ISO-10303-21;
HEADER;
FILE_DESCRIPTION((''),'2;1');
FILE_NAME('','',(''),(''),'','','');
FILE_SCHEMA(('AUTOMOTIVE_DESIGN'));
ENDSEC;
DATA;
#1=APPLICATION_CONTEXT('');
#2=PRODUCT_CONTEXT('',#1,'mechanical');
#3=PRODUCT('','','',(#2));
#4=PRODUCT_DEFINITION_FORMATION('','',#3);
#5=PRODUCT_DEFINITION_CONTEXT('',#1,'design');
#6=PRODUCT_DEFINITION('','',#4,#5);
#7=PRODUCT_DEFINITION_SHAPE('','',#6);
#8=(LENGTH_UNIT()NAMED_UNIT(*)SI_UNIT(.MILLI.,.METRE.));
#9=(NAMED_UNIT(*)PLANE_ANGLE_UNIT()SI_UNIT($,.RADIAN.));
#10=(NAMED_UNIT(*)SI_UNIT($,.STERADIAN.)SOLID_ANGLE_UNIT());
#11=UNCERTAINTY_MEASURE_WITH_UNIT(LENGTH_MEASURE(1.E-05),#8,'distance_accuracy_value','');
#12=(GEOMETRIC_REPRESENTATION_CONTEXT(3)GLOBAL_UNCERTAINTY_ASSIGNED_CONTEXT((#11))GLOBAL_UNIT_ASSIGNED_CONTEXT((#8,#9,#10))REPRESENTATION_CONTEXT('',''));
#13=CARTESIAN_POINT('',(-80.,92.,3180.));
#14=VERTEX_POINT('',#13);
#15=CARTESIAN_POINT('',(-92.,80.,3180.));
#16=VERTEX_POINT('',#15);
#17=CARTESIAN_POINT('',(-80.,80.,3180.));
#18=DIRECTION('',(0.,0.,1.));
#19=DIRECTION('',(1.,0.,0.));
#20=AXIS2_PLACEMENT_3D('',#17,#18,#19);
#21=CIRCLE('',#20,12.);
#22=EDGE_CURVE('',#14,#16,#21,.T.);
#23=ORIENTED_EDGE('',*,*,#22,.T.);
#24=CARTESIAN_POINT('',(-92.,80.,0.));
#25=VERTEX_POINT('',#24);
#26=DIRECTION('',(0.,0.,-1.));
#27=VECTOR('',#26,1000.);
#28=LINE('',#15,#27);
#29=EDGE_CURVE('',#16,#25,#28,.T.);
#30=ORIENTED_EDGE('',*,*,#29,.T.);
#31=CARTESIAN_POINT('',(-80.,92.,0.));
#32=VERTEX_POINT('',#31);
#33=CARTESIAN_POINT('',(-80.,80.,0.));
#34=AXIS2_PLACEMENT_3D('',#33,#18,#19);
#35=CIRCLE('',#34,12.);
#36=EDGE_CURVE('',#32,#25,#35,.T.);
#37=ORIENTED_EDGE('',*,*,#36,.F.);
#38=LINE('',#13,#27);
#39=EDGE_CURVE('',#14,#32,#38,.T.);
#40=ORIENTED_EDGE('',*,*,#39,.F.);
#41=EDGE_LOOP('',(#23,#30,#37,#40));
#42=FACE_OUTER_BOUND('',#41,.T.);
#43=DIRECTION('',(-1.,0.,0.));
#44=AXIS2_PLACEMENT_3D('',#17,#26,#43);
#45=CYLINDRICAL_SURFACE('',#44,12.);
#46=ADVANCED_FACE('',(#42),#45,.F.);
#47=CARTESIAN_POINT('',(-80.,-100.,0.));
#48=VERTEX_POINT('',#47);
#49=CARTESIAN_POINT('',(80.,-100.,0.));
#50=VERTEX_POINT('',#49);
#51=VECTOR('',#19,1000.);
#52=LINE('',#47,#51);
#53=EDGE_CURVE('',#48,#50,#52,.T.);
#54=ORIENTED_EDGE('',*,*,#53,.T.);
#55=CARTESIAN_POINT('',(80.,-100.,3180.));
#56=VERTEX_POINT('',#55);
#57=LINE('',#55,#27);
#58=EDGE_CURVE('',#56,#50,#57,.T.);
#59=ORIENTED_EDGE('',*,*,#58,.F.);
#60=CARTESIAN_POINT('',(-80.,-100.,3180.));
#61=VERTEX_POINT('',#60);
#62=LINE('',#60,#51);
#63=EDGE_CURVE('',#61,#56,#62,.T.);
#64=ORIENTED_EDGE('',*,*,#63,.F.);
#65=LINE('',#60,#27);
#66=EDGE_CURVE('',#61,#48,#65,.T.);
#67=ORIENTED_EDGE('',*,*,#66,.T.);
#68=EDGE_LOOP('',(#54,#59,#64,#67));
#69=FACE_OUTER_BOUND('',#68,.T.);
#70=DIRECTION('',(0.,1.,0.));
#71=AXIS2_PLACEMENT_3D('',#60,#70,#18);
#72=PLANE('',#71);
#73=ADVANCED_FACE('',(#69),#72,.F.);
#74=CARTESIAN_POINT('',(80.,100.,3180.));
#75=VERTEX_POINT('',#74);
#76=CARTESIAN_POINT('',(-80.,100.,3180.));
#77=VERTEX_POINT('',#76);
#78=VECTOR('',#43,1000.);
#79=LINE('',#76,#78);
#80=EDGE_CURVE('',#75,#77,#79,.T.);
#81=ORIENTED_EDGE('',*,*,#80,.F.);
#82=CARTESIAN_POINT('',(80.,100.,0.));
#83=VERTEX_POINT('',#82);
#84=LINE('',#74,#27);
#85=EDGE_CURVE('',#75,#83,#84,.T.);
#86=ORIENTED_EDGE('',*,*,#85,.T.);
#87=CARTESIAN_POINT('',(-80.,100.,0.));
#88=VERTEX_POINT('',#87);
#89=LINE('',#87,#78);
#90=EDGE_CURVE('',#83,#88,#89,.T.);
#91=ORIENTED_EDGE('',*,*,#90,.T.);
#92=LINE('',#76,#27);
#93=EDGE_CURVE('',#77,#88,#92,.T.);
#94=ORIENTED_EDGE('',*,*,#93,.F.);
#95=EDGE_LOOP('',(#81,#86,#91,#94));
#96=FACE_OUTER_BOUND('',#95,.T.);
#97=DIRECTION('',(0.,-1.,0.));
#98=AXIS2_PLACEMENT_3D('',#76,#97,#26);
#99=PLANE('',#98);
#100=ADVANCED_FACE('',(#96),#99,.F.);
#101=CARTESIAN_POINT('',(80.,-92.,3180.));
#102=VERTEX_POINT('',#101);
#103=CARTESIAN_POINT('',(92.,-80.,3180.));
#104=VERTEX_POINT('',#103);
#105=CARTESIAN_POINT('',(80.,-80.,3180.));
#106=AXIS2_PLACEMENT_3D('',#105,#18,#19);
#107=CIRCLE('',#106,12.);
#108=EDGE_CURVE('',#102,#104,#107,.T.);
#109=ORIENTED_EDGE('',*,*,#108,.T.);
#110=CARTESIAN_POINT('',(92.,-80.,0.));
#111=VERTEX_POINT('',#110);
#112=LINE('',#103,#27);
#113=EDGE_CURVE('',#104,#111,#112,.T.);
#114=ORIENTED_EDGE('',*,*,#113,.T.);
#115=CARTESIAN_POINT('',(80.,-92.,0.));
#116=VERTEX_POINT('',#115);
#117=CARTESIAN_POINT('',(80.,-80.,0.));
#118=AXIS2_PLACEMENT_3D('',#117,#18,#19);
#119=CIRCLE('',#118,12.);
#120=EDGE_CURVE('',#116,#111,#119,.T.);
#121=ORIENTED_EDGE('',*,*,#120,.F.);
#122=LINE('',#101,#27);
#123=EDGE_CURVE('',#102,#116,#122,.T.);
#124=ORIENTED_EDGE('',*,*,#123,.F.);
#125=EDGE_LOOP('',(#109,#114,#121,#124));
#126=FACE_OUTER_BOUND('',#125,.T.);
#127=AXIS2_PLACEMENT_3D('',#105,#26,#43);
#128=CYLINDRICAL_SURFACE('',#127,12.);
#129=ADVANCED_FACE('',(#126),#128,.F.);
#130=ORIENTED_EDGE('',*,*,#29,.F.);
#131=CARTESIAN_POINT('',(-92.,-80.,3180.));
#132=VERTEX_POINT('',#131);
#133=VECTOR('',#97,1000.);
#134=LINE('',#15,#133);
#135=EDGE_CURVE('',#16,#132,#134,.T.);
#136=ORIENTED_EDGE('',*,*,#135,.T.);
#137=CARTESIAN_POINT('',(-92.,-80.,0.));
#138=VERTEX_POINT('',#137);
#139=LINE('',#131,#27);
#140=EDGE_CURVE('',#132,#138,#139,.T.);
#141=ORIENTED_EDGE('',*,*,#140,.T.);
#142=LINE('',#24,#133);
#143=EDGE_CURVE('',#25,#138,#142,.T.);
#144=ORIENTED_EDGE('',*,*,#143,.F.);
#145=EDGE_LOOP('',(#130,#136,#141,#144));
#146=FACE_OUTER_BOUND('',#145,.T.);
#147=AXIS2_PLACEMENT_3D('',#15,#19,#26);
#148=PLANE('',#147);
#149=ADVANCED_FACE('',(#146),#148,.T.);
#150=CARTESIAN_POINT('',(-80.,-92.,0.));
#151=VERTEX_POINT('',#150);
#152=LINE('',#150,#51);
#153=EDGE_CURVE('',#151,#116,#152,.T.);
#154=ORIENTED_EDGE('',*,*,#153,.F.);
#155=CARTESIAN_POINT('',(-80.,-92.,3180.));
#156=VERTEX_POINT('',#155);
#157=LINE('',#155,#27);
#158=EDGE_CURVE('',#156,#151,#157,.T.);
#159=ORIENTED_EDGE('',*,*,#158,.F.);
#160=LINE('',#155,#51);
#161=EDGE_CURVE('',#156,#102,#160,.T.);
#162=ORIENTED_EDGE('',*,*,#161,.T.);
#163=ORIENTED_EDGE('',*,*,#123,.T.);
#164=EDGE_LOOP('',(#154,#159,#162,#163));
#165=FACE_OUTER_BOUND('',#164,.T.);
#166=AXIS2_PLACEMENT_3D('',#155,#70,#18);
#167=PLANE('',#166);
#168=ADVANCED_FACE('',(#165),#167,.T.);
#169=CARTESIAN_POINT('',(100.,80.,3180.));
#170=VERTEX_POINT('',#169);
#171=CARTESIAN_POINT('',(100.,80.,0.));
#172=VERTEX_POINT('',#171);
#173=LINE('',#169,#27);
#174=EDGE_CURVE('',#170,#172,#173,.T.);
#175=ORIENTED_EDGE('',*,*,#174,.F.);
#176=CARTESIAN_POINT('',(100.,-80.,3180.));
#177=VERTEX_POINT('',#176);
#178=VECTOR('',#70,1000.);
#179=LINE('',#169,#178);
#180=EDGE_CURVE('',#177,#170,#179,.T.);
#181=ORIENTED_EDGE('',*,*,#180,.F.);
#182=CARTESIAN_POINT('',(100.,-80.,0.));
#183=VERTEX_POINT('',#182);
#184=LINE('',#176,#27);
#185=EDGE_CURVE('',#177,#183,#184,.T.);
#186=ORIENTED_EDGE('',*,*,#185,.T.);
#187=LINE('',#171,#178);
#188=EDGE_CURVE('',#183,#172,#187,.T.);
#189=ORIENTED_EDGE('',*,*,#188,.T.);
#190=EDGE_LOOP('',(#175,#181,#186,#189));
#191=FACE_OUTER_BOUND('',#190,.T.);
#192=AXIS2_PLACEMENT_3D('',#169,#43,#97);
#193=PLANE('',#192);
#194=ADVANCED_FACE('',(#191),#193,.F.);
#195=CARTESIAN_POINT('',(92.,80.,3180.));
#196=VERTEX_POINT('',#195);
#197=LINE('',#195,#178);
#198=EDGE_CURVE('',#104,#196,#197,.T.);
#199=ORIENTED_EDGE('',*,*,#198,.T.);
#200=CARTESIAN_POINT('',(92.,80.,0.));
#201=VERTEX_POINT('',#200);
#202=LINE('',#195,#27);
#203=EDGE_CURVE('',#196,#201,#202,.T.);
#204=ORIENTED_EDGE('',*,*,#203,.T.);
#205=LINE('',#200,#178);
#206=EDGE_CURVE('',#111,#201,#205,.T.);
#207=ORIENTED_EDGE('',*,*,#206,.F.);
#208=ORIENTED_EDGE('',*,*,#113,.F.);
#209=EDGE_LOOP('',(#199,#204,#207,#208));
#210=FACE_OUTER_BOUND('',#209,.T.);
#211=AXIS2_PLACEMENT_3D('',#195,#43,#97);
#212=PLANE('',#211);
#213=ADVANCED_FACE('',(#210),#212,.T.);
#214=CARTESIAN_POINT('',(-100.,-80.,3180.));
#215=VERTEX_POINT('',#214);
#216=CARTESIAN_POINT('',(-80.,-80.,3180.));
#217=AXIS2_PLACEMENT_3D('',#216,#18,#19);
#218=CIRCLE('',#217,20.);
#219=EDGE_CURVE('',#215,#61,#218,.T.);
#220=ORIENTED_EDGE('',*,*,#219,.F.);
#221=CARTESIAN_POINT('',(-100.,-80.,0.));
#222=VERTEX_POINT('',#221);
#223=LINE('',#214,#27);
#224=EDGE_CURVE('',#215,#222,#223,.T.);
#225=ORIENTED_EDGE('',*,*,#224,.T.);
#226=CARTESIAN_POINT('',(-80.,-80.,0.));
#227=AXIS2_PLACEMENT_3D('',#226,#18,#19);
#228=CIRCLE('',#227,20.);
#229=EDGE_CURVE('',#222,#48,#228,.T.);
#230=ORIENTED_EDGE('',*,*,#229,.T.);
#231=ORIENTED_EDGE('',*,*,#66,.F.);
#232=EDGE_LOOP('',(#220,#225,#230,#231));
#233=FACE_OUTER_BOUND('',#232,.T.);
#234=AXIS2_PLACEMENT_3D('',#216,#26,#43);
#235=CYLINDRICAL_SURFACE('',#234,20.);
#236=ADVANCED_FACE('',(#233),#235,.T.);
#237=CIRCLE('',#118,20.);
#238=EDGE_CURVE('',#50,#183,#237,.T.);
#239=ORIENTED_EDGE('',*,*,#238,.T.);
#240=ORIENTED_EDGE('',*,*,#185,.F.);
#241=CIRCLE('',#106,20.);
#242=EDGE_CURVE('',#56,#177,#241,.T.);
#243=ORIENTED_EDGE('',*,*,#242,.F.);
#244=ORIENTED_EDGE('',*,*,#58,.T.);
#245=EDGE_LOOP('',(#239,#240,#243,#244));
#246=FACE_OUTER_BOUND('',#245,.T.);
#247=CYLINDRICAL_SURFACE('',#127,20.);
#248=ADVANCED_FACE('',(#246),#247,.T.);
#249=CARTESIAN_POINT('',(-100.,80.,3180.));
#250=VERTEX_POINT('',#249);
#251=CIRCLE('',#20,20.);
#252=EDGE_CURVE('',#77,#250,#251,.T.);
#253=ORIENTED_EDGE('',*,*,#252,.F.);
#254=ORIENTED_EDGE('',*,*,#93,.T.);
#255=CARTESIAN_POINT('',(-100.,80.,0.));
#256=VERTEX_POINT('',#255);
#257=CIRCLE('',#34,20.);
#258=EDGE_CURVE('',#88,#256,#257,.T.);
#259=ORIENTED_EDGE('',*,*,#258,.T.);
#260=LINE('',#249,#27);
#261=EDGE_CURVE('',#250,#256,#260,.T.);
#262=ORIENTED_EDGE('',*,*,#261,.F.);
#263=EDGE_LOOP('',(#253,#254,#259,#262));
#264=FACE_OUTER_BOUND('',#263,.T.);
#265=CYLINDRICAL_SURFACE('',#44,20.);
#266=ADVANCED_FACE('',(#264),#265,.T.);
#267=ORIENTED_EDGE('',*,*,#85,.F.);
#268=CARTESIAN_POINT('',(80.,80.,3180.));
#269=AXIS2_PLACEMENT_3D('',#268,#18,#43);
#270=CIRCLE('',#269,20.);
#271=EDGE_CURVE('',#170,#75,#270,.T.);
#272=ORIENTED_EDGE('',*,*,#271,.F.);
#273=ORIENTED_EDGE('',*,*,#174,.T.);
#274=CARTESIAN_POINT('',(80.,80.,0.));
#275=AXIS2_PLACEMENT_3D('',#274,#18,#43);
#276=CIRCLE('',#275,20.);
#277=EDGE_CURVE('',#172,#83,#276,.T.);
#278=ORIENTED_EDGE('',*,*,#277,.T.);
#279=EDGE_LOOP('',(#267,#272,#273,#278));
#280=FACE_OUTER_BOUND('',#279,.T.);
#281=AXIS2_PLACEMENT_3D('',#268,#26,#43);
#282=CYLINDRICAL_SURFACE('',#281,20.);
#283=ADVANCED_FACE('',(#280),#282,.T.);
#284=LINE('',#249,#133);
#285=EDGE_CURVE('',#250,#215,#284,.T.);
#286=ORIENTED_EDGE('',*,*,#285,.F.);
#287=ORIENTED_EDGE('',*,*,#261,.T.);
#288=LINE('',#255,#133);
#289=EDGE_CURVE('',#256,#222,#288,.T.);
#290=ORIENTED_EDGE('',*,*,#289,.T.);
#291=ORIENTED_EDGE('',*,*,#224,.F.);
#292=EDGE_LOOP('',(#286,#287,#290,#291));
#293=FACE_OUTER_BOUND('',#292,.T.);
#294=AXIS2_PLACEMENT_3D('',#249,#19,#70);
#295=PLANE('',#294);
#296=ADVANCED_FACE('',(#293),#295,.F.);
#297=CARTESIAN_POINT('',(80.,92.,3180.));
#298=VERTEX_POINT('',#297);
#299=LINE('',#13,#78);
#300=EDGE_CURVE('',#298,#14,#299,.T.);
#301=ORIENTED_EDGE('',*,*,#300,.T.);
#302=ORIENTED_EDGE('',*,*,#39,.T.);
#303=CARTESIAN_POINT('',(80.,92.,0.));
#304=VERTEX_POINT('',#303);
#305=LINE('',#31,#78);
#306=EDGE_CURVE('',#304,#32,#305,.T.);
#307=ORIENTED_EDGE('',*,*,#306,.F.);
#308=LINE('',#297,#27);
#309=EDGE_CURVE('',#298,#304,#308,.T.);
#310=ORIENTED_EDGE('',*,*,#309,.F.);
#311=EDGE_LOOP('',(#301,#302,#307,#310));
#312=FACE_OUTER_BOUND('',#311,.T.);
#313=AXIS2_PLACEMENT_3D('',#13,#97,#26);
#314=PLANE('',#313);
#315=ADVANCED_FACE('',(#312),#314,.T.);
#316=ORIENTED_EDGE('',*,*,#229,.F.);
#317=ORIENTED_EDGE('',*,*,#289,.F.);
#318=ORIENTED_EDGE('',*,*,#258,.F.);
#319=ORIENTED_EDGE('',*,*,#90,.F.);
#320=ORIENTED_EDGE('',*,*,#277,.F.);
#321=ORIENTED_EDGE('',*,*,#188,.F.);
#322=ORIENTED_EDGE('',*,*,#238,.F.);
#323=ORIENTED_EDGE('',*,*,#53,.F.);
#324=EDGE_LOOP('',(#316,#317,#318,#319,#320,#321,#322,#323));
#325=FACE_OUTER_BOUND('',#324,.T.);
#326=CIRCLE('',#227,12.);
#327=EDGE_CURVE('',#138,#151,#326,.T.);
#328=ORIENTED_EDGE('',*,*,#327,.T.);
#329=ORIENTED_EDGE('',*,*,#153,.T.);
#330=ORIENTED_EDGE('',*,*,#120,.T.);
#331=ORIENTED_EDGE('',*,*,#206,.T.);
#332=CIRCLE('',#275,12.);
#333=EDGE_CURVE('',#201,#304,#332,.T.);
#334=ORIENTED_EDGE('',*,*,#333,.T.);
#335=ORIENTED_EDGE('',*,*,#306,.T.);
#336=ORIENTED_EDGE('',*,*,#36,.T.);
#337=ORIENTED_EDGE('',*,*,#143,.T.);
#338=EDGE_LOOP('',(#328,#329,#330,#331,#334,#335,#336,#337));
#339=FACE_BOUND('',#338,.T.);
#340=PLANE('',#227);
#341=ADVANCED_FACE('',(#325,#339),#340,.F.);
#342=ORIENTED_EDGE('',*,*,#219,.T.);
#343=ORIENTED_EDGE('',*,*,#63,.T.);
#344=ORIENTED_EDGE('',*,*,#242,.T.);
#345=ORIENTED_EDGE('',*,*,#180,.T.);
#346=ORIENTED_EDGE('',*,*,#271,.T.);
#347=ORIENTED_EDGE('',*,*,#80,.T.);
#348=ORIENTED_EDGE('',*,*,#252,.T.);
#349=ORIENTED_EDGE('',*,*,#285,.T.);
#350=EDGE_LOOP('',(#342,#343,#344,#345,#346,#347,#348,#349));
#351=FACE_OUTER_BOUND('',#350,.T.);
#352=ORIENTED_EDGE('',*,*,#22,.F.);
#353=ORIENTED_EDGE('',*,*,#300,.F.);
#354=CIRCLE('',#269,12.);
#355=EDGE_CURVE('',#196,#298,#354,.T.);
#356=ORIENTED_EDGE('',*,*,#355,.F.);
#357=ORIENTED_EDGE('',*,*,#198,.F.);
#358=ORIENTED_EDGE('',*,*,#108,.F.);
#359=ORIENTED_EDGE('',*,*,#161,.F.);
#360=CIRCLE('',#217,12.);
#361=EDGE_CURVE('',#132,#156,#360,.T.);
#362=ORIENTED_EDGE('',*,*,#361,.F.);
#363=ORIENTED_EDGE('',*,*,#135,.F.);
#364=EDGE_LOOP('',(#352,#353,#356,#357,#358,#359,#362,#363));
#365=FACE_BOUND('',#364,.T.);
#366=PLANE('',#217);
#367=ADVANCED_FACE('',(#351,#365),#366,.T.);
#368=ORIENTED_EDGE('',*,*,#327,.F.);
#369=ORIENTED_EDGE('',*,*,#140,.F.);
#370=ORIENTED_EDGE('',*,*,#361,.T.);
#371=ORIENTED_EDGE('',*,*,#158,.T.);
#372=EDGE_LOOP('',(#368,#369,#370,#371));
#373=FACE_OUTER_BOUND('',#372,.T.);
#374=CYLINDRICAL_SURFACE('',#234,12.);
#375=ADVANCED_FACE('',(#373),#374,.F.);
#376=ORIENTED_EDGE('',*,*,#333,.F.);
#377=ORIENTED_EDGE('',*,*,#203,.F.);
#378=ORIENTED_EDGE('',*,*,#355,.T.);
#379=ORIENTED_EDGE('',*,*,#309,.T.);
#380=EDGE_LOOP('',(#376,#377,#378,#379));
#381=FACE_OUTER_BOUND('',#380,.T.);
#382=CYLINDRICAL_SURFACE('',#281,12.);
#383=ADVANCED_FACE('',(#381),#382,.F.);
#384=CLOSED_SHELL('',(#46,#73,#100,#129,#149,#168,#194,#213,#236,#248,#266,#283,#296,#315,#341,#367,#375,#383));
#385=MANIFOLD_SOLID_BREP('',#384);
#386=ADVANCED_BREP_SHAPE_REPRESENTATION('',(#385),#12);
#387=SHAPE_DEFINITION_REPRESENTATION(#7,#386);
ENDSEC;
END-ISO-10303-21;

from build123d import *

# Parameters (mm, degrees)
BOSS_EXTRUDE1_DEPTH = 3180


with BuildPart() as part:
    # Sketch1 → Boss-Extrude1 (new body)
    with BuildSketch(Plane.XY):
        with BuildLine():
            Line((-80, 100), (80, 100))
            ThreePointArc((80, 100), (94.142135624, 94.142135624), (100, 80))
            Line((100, 80), (100, -80))
            ThreePointArc((100, -80), (94.142135624, -94.142135624), (80, -100))
            Line((80, -100), (-80, -100))
            ThreePointArc((-80, -100), (-94.142135624, -94.142135624), (-100, -80))
            Line((-100, -80), (-100, 80))
            ThreePointArc((-100, 80), (-94.142135624, 94.142135624), (-80, 100))
        make_face()
        with BuildLine():
            Line((-92, 80), (-92, -80))
            ThreePointArc((-92, -80), (-88.485281374, -88.485281374), (-80, -92))
            Line((-80, -92), (80, -92))
            ThreePointArc((80, -92), (88.485281374, -88.485281374), (92, -80))
            Line((92, -80), (92, 80))
            ThreePointArc((92, 80), (88.485281374, 88.485281374), (80, 92))
            Line((80, 92), (-80, 92))
            ThreePointArc((-80, 92), (-88.485281374, 88.485281374), (-92, 80))
        make_face(mode=Mode.SUBTRACT)
    extrude(amount=BOSS_EXTRUDE1_DEPTH)


solid = part.part
